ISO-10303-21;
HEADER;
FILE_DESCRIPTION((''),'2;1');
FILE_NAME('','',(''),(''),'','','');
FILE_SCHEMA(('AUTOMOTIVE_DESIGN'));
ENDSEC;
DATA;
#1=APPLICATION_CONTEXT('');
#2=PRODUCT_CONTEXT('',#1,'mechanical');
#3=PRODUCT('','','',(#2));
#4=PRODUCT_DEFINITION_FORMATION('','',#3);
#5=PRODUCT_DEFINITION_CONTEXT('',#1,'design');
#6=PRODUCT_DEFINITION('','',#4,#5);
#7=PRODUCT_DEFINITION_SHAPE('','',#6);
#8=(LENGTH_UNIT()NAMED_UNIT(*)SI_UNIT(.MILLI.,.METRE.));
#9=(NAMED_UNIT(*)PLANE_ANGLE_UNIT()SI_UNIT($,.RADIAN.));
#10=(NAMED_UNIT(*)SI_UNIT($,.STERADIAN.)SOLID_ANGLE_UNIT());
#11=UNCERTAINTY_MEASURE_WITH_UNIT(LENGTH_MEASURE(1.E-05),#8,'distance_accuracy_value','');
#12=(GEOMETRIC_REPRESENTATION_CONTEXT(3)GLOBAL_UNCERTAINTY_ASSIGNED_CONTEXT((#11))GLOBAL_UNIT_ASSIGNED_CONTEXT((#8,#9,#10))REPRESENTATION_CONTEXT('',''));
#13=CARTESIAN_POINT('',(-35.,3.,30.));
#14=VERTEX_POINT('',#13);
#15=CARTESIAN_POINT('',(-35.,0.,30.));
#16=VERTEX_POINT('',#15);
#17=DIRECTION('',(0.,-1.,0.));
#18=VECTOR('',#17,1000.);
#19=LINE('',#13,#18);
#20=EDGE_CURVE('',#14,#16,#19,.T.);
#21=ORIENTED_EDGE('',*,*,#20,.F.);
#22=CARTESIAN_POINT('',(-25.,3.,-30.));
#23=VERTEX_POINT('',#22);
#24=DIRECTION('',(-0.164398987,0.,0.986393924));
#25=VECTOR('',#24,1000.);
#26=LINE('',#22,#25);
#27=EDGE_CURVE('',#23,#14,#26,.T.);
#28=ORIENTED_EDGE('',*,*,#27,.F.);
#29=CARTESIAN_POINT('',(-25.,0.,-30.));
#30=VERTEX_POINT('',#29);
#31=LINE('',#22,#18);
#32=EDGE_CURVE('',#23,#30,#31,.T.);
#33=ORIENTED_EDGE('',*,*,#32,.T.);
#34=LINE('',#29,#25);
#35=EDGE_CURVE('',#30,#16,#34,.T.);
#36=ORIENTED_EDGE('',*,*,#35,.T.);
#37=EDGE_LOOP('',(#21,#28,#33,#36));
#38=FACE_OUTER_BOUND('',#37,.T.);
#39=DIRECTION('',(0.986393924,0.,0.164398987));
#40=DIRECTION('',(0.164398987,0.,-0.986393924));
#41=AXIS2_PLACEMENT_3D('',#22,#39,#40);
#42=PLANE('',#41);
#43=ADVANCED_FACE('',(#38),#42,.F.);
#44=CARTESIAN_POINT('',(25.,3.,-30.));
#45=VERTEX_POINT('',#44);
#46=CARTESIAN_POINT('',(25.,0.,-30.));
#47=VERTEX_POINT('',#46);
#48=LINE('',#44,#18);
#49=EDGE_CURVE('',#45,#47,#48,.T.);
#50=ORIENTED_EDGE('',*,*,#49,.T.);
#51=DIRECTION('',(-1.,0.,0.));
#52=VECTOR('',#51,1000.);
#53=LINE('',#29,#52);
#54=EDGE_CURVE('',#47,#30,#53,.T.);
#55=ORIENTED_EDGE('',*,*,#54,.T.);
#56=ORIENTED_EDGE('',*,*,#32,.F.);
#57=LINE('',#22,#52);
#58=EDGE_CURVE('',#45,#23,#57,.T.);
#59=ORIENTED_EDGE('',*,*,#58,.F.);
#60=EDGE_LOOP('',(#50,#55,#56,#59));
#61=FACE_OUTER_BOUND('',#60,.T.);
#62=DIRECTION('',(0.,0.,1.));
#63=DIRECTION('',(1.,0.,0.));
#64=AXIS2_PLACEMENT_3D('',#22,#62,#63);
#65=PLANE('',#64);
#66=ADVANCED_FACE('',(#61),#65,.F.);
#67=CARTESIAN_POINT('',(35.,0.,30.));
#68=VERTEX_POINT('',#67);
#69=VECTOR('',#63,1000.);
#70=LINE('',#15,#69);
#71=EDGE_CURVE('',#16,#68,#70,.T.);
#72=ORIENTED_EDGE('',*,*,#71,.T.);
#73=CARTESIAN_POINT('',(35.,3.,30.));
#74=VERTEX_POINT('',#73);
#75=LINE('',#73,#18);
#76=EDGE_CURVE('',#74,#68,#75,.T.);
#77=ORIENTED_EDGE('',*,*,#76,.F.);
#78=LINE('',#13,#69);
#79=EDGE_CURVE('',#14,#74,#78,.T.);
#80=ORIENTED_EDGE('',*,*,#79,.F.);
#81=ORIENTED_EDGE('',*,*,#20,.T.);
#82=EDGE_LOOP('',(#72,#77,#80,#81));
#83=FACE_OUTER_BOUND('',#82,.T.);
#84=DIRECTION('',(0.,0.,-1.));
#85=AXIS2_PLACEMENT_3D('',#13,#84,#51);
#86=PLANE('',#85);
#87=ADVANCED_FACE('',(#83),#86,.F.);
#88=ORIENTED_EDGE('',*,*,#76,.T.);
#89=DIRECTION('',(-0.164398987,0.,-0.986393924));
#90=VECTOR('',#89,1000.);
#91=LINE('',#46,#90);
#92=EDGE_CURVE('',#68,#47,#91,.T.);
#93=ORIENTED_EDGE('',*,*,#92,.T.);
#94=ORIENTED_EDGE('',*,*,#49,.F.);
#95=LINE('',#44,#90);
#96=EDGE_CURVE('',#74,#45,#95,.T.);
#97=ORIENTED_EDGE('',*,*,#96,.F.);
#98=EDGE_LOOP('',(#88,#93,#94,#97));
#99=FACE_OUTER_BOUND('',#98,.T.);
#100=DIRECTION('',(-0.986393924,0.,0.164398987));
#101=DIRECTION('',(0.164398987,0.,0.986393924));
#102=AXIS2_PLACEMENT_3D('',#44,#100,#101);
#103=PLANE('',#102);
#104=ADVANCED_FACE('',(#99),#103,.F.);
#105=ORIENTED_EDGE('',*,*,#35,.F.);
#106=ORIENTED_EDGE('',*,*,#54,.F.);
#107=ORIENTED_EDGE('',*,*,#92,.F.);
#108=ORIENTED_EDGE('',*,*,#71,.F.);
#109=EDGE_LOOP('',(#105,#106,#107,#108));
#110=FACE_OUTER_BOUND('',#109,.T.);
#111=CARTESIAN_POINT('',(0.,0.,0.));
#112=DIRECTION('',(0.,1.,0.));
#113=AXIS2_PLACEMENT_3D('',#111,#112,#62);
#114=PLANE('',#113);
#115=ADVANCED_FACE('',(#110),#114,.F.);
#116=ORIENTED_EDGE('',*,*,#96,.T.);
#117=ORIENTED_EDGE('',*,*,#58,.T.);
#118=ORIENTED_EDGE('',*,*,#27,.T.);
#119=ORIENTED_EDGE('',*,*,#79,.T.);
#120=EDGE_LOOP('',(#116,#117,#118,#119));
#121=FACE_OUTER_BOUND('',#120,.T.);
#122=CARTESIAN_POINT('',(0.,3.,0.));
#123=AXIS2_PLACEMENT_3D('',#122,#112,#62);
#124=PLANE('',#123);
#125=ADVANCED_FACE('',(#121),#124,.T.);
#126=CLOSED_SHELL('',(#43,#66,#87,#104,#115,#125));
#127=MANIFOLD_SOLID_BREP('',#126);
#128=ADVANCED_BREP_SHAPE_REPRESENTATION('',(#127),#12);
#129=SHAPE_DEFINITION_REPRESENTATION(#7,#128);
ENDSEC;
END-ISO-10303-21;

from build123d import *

# Parameters (mm, degrees)
BOSS_EXTRUDE1_DEPTH = 3


with BuildPart() as part:
    # Sketch1 → Boss-Extrude1 (new body)
    with BuildSketch(Plane(origin=(0, 0, 0), x_dir=(1, 0, 0), z_dir=(0, 1, 0))):
        Polygon((-25, 30), (25, 30), (35, -30), (-35, -30), align=None)
    extrude(amount=BOSS_EXTRUDE1_DEPTH)


solid = part.part
